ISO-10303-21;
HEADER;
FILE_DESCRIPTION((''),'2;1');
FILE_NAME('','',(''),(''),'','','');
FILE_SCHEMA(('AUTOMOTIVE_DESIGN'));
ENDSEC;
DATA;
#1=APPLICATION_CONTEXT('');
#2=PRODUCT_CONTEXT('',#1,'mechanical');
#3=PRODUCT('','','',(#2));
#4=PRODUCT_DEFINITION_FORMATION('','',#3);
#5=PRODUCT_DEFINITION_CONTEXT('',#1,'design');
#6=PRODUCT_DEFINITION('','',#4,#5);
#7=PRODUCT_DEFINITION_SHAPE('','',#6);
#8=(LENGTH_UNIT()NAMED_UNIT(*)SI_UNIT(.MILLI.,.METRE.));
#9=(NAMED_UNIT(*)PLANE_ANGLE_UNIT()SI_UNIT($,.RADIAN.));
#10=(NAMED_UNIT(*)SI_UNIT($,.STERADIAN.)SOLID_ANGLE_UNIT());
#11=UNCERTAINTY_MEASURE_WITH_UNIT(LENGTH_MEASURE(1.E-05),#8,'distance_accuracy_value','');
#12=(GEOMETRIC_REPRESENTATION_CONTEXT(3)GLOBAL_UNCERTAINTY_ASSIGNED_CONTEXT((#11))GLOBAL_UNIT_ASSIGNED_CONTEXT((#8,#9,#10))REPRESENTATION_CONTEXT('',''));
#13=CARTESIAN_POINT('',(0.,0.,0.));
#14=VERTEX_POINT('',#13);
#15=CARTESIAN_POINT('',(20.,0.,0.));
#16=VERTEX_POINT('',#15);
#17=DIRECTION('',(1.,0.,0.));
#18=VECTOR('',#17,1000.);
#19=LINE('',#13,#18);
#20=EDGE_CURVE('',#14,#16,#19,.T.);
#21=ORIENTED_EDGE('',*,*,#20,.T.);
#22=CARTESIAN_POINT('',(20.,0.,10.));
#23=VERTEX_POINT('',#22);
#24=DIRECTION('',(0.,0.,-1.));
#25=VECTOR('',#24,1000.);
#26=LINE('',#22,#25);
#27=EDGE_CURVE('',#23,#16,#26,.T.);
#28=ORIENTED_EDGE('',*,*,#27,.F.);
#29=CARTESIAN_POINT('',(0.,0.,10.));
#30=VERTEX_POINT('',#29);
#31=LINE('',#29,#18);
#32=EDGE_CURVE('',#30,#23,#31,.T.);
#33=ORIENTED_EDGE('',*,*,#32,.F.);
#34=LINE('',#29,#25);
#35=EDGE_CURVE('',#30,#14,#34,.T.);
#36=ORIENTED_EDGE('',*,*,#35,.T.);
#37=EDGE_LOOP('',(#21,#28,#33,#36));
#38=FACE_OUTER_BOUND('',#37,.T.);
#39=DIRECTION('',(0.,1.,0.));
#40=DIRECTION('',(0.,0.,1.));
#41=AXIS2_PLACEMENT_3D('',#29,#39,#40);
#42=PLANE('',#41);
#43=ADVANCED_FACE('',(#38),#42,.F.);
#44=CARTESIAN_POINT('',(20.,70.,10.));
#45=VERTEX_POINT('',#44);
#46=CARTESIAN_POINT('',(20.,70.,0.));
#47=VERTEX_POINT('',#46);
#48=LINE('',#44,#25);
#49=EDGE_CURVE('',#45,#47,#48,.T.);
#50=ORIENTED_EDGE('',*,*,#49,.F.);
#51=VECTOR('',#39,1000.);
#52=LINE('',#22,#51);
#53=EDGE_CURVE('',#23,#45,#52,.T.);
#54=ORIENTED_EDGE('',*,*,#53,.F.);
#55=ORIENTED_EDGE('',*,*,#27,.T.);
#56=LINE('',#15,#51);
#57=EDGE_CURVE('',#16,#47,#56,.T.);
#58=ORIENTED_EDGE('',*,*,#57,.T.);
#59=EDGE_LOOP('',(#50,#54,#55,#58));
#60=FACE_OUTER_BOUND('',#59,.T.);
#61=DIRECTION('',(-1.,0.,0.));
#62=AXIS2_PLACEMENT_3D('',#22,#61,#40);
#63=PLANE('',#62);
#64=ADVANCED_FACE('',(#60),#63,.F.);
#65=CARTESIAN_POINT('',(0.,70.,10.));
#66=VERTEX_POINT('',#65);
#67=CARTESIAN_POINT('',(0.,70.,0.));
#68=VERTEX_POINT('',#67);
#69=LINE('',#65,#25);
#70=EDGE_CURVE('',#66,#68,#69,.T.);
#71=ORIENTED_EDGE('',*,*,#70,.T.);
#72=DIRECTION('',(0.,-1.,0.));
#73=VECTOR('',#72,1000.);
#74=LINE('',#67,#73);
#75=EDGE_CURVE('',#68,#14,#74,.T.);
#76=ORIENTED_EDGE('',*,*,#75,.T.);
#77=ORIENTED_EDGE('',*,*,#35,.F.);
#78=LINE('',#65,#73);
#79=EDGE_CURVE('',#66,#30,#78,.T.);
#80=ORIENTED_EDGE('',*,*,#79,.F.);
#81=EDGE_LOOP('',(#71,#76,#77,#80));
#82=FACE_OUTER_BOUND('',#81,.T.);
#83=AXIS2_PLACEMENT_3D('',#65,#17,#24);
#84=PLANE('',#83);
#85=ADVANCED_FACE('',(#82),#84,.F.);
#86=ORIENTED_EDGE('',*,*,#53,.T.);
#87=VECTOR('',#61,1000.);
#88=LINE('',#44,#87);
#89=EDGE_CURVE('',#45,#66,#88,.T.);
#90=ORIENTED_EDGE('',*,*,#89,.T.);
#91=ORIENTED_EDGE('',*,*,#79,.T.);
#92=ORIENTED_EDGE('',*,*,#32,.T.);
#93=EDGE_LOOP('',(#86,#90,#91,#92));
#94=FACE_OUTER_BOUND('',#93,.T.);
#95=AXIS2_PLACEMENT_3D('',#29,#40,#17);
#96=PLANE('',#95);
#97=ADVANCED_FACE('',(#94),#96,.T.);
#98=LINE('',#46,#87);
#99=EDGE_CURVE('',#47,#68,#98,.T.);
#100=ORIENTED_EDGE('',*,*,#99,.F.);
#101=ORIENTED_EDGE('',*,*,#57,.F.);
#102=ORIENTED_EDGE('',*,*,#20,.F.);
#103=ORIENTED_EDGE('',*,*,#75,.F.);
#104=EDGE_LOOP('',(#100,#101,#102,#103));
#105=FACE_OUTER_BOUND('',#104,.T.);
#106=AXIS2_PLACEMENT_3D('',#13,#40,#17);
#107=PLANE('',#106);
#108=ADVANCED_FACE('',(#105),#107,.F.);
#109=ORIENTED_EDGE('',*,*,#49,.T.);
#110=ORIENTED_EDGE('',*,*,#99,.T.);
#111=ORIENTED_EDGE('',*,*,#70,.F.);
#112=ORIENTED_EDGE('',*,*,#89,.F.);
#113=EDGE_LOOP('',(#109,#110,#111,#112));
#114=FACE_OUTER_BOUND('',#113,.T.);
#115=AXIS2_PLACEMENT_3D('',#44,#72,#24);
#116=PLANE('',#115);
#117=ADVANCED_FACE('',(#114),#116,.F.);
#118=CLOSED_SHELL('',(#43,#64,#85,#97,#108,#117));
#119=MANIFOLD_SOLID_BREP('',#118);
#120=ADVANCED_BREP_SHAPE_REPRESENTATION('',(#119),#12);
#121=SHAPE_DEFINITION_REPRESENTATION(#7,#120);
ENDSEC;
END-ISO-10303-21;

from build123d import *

# Parameters (mm, degrees)
SKETCH_1_W      = 20
SKETCH_1_H      = 70
EXTRUDE_1_DEPTH = 10


with BuildPart() as part:
    # 草图1 → 凸台-拉伸1 (new body)
    with BuildSketch(Plane.XY):
        with Locations((10, 35)):
            Rectangle(SKETCH_1_W, SKETCH_1_H)
    extrude(amount=EXTRUDE_1_DEPTH)


solid = part.part
